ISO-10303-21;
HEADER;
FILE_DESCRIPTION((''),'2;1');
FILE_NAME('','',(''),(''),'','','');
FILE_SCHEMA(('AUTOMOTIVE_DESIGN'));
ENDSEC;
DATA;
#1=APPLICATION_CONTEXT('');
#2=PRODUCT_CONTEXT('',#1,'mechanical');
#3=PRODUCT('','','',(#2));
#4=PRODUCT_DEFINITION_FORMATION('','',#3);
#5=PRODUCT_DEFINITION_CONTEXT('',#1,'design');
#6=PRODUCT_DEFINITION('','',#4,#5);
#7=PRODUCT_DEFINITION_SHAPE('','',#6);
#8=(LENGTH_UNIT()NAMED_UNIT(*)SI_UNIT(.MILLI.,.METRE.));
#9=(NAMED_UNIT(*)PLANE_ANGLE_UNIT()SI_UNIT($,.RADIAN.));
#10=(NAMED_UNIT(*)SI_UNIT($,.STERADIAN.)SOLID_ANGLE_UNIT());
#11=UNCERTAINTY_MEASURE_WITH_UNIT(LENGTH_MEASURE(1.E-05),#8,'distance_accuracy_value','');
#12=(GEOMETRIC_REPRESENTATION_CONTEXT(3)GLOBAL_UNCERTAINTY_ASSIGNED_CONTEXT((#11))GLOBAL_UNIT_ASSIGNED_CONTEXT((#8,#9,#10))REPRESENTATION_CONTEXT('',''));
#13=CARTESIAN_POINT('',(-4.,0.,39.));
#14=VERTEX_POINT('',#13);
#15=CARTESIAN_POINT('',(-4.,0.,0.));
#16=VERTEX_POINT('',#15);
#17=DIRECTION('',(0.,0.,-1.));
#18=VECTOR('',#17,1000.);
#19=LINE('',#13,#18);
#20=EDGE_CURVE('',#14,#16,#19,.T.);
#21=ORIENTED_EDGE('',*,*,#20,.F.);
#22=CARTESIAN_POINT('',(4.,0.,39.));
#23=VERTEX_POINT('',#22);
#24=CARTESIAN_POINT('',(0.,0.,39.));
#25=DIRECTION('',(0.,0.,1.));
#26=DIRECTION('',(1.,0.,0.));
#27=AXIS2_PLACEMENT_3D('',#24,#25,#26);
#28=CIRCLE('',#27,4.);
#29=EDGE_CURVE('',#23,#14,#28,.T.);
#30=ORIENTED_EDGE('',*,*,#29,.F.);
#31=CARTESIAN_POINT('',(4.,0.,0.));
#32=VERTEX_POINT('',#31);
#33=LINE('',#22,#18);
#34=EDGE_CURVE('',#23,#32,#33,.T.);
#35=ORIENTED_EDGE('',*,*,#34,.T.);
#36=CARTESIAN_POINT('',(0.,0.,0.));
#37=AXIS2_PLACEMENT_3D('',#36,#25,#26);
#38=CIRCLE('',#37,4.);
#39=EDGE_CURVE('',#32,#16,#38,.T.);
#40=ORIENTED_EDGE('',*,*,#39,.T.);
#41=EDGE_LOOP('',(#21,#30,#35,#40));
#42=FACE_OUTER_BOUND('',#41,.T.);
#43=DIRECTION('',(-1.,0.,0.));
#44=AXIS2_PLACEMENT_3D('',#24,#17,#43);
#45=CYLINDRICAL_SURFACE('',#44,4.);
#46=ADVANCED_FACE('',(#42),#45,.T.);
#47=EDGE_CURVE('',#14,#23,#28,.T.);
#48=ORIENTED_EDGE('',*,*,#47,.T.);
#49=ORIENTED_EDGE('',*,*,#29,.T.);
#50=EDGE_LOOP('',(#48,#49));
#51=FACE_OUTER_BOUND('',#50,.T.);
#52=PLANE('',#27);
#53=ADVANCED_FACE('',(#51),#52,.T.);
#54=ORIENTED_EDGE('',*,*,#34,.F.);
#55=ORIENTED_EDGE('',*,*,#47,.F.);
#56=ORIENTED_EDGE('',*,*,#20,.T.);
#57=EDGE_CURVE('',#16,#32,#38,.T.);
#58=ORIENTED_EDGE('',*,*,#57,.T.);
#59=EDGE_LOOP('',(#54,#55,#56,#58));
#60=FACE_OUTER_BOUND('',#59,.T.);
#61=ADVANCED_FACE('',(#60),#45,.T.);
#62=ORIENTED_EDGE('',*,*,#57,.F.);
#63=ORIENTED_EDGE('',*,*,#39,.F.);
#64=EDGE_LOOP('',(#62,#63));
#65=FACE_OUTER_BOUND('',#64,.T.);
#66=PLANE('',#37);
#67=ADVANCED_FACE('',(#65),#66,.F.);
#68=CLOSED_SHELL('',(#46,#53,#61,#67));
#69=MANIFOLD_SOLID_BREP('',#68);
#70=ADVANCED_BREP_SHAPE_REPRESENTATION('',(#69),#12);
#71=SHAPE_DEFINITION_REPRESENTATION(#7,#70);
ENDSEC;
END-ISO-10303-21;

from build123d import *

# Parameters (mm, degrees)
SKETCH_1_R      = 4
EXTRUDE_1_DEPTH = 39


with BuildPart() as part:
    # 草图1 → 凸台-拉伸1 (new body)
    with BuildSketch(Plane.XY):
        Circle(SKETCH_1_R)
    extrude(amount=EXTRUDE_1_DEPTH)


solid = part.part
